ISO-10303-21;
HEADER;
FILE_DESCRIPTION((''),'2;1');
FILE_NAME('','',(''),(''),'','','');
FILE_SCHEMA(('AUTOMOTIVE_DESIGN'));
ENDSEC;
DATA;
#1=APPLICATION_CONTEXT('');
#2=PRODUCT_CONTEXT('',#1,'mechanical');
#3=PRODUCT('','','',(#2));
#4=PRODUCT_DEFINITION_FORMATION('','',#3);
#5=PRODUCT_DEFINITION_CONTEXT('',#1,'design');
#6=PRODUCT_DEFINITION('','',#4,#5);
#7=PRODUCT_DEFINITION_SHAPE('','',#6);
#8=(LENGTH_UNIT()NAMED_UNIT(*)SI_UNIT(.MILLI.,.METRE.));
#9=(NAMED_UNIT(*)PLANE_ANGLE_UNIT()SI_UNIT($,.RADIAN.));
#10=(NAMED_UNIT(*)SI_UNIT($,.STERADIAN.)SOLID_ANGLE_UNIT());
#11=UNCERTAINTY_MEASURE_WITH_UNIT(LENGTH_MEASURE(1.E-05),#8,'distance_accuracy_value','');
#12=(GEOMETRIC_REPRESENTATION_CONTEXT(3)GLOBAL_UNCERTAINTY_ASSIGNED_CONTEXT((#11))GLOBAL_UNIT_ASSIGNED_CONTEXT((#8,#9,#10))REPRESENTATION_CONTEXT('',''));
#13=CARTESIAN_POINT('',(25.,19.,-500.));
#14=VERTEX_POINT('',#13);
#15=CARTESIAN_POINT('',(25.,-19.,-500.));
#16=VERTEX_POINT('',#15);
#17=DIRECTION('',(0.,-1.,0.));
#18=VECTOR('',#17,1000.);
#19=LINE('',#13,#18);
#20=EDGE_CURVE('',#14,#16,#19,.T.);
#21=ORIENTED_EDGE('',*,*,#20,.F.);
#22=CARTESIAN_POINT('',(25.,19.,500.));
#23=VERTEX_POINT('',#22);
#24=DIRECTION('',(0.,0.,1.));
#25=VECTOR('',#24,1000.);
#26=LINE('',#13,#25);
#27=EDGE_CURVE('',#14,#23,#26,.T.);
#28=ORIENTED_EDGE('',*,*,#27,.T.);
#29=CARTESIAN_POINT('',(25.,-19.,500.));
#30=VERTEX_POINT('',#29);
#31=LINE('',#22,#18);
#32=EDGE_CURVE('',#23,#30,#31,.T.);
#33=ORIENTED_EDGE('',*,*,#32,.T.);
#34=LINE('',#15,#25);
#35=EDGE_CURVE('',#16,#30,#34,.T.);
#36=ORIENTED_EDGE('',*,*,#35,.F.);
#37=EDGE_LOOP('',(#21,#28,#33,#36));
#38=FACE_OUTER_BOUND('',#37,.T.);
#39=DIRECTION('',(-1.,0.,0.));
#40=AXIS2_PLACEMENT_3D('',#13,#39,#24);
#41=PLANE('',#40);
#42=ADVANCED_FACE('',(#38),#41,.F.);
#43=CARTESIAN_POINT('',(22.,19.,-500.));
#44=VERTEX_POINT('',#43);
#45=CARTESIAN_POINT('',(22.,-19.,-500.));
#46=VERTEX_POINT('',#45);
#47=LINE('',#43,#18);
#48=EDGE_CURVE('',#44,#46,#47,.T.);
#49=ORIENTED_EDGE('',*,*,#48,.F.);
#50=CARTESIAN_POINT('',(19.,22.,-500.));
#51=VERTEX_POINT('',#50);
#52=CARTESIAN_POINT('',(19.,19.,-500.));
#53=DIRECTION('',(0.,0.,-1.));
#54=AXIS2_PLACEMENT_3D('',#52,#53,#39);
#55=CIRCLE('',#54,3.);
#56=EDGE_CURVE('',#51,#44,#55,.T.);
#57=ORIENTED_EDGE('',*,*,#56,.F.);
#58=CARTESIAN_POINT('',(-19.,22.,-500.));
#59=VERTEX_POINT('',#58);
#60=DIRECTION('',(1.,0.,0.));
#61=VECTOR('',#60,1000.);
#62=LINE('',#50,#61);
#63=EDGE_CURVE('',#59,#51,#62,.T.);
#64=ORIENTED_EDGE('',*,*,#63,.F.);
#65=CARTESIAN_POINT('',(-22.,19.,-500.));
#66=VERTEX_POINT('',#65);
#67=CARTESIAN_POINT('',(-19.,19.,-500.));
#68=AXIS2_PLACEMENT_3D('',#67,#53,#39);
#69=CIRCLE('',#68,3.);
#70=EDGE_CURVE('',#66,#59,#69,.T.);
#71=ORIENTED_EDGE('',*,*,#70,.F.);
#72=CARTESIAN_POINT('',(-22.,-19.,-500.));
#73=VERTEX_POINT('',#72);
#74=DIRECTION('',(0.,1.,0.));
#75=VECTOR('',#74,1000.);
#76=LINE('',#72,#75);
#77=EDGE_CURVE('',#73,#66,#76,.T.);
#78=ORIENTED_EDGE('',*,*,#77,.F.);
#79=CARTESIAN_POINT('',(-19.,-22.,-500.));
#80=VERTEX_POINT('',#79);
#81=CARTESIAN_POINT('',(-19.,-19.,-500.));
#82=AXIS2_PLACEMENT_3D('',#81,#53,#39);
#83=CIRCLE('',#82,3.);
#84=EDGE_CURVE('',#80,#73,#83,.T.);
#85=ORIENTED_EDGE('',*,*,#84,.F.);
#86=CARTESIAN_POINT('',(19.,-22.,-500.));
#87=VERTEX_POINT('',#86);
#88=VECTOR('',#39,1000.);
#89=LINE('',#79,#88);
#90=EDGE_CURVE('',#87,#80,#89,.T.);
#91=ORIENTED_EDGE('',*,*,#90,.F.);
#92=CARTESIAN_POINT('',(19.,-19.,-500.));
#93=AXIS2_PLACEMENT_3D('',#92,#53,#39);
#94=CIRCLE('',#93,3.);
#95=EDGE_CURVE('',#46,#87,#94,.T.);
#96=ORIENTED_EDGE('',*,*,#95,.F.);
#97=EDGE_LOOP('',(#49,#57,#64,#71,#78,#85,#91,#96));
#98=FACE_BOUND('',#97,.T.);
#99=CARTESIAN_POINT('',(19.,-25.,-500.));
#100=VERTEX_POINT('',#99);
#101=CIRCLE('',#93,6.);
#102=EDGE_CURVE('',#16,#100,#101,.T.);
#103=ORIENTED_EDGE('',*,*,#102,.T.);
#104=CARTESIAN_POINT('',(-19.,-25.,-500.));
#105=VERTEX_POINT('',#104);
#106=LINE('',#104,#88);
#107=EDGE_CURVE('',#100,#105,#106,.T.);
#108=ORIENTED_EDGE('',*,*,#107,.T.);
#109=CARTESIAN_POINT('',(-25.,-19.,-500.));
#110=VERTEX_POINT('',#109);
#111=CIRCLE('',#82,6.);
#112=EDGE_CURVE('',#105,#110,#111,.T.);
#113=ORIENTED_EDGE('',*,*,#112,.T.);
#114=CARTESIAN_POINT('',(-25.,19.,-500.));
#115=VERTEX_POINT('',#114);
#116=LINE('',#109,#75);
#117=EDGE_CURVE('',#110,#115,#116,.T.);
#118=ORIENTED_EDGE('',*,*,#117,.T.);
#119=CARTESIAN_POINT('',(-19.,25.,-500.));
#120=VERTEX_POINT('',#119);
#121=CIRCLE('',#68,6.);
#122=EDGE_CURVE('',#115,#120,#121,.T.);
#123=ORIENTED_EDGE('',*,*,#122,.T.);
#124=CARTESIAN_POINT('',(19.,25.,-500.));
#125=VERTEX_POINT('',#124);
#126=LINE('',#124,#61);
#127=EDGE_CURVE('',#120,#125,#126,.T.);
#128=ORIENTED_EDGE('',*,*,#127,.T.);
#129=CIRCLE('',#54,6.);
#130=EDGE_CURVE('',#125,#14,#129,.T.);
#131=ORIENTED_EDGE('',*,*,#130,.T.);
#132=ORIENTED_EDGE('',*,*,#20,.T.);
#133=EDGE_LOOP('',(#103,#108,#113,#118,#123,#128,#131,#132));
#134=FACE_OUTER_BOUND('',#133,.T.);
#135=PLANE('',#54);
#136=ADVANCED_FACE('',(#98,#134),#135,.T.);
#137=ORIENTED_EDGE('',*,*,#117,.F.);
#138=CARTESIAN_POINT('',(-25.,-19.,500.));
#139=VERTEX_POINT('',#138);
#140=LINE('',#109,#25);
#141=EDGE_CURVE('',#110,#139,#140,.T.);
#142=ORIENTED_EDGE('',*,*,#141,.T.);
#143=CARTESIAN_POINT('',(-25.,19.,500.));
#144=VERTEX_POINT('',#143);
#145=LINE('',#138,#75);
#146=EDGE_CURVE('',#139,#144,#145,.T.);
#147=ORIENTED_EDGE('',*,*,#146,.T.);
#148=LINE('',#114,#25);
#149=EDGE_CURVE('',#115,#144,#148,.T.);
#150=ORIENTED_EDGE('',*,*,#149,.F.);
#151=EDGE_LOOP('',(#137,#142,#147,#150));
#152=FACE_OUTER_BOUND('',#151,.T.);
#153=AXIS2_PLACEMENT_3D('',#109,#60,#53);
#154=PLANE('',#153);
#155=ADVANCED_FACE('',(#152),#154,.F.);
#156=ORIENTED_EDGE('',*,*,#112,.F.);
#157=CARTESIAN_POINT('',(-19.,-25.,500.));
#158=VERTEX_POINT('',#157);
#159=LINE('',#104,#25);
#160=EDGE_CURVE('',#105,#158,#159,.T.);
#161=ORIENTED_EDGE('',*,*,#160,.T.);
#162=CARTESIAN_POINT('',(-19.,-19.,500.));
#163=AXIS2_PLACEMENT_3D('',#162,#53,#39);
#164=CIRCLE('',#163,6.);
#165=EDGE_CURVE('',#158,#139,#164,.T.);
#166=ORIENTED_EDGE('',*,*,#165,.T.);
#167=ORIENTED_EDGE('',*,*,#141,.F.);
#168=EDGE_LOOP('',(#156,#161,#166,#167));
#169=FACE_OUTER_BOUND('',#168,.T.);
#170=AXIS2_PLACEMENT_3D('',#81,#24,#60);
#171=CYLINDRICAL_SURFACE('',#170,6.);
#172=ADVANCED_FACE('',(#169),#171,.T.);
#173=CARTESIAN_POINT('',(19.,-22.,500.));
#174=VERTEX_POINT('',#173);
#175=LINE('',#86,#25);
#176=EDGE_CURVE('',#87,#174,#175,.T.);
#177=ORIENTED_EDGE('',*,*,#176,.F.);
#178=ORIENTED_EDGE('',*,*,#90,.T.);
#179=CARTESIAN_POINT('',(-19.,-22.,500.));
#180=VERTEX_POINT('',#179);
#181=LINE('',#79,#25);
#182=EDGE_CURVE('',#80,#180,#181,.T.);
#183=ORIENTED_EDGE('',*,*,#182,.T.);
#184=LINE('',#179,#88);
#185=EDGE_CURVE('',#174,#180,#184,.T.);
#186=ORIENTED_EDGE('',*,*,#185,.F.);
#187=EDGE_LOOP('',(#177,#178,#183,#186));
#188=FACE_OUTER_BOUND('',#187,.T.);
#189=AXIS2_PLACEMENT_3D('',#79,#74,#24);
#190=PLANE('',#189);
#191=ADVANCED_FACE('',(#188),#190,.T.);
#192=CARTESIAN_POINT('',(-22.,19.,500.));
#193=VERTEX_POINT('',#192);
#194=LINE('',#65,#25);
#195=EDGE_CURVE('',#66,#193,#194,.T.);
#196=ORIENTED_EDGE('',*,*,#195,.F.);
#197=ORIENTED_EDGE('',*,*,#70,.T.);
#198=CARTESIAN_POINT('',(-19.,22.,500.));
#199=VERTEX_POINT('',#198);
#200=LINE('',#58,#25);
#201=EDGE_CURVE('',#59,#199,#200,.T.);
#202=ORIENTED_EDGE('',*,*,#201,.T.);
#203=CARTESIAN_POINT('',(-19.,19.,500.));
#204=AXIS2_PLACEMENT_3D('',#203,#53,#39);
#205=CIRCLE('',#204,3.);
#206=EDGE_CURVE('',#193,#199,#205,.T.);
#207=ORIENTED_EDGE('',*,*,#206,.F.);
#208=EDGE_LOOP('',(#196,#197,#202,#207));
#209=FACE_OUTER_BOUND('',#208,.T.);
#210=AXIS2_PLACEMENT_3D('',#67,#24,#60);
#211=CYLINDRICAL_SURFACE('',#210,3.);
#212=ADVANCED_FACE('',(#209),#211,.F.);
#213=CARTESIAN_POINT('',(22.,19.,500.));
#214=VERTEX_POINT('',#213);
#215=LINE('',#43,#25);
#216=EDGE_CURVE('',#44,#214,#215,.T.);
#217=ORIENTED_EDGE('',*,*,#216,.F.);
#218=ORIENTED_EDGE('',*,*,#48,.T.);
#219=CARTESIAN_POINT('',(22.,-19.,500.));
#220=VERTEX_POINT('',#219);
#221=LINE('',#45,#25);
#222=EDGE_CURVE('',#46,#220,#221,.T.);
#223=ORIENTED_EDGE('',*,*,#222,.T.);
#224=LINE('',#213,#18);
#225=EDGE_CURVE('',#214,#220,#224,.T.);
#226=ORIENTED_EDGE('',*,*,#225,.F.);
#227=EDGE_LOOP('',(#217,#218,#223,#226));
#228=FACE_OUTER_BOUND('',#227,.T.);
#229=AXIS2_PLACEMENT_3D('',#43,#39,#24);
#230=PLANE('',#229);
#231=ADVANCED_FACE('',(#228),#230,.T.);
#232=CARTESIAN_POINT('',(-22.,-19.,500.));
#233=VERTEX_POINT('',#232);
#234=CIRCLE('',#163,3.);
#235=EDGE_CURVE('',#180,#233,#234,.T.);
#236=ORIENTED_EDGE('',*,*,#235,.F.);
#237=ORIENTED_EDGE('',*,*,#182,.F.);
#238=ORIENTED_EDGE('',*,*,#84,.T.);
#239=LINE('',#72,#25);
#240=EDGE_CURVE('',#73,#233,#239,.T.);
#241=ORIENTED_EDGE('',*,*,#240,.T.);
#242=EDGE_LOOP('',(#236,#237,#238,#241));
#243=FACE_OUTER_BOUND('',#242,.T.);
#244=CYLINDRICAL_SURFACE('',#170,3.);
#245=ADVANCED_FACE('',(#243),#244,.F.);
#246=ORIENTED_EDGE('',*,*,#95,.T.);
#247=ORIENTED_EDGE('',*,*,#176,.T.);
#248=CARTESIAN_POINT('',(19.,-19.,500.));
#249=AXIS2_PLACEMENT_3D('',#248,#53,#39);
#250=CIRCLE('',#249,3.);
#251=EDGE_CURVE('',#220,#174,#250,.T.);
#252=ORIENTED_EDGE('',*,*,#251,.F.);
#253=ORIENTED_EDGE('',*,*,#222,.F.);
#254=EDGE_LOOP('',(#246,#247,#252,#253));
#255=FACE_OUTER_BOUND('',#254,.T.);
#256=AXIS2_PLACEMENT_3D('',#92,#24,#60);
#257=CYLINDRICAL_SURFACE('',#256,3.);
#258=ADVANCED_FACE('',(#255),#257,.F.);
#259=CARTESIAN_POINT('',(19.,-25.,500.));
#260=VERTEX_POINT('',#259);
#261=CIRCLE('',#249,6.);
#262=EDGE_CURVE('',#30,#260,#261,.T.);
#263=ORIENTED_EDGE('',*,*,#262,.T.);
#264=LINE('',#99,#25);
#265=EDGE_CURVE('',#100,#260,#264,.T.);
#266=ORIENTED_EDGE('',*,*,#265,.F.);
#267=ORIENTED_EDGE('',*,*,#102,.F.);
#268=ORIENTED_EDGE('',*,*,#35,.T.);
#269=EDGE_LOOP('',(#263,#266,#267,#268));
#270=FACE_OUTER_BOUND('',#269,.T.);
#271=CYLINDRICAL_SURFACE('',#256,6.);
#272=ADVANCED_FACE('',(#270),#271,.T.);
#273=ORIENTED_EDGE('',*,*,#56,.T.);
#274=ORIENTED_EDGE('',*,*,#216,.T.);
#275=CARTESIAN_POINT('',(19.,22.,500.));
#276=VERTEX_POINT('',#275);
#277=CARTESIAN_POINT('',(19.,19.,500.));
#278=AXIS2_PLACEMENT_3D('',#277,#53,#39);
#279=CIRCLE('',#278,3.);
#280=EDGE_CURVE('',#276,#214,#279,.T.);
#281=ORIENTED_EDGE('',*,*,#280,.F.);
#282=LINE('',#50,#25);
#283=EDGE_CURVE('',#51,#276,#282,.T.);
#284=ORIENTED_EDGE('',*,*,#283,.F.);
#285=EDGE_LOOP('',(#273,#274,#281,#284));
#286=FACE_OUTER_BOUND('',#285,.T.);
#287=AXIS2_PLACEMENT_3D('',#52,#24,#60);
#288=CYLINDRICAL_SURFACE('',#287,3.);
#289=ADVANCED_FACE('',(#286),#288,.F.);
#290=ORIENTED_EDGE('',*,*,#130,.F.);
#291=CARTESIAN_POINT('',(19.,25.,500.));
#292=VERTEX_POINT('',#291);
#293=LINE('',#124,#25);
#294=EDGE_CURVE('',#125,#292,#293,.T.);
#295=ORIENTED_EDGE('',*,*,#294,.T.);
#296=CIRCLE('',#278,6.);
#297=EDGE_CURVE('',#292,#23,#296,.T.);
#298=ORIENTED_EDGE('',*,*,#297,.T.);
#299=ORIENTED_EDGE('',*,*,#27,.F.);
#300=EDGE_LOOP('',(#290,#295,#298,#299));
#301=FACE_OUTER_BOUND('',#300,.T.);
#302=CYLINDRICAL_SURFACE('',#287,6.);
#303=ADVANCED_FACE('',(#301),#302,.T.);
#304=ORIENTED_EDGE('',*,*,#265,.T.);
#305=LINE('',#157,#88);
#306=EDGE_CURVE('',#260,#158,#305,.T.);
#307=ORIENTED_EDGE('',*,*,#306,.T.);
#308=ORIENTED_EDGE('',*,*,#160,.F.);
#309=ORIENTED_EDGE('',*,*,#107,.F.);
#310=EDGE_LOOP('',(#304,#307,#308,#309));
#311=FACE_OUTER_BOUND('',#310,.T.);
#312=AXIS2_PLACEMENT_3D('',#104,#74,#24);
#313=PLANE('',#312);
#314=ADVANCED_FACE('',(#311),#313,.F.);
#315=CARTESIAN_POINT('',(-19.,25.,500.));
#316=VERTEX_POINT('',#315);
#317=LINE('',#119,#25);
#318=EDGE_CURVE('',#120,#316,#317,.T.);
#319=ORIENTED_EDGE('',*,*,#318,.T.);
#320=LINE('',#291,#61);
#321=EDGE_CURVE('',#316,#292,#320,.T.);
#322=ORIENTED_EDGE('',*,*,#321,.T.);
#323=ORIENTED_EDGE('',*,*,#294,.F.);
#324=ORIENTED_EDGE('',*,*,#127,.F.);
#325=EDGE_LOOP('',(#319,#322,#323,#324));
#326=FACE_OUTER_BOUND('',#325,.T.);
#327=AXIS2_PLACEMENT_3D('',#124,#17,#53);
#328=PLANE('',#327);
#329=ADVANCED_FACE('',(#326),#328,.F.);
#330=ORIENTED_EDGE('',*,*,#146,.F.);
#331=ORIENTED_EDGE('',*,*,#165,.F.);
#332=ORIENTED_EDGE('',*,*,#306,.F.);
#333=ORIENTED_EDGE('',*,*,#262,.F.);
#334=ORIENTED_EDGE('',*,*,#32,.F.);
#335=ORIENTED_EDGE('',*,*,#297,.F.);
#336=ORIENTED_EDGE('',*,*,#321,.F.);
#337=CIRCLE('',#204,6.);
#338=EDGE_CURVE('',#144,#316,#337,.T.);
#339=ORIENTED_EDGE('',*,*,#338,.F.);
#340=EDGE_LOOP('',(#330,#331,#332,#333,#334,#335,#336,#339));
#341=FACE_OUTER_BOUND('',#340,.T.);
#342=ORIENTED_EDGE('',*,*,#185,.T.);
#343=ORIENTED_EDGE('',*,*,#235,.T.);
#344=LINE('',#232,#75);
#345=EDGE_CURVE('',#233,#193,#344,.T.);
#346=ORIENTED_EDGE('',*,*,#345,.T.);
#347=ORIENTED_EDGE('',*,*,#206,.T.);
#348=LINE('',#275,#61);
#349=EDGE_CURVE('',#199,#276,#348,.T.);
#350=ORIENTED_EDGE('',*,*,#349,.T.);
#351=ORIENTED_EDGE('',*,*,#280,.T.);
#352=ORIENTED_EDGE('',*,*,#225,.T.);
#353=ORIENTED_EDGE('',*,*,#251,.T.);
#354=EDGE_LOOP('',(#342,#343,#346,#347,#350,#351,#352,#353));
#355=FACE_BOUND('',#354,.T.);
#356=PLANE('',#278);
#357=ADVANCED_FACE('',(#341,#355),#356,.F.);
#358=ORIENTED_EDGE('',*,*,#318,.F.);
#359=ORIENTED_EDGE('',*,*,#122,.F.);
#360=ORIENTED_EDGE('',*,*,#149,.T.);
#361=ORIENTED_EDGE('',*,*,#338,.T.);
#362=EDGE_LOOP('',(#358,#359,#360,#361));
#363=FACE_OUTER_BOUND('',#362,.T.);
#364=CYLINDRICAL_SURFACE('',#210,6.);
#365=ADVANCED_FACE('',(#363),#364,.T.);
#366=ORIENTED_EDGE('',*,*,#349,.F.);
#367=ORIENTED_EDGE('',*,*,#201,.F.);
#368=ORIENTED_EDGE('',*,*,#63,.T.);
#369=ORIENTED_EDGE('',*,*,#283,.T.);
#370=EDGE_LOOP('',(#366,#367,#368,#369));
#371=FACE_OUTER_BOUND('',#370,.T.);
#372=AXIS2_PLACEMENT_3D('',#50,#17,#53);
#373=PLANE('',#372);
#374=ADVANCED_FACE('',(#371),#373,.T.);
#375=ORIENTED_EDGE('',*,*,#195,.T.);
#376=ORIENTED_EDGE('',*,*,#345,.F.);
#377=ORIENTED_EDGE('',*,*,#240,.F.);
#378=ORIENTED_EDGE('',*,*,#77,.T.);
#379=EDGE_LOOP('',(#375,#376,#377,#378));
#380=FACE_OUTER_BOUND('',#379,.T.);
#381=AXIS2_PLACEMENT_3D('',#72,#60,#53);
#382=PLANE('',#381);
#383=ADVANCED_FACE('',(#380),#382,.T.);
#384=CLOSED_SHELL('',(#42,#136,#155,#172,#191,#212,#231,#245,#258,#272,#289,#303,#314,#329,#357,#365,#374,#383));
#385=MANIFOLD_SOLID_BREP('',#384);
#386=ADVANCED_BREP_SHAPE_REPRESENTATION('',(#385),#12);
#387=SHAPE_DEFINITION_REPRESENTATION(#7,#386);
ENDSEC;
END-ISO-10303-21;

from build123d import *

# Parameters (mm, degrees)
GB_6728_1986_050_X_50_X_3_1_DEPTH = 1000


with BuildPart() as part:
    # Sketch1 → Gb／6728-1986方形空心型钢 050 X 50 X 3(1) (new body)
    with BuildSketch(Plane.YX.offset(-500)):
        with BuildLine():
            Line((-19, -25), (19, -25))
            ThreePointArc((19, -25), (23.242640687, -23.242640687), (25, -19))
            Line((25, -19), (25, 19))
            ThreePointArc((25, 19), (23.242640687, 23.242640687), (19, 25))
            Line((19, 25), (-19, 25))
            ThreePointArc((-19, 25), (-23.242640687, 23.242640687), (-25, 19))
            Line((-25, 19), (-25, -19))
            ThreePointArc((-25, -19), (-23.242640687, -23.242640687), (-19, -25))
        make_face()
        with BuildLine():
            Line((-19, -22), (19, -22))
            ThreePointArc((19, -22), (21.121320344, -21.121320344), (22, -19))
            Line((22, -19), (22, 19))
            ThreePointArc((22, 19), (21.121320344, 21.121320344), (19, 22))
            Line((19, 22), (-19, 22))
            ThreePointArc((-19, 22), (-21.121320344, 21.121320344), (-22, 19))
            Line((-22, 19), (-22, -19))
            ThreePointArc((-22, -19), (-21.121320344, -21.121320344), (-19, -22))
        make_face(mode=Mode.SUBTRACT)
    extrude(amount=GB_6728_1986_050_X_50_X_3_1_DEPTH)


solid = part.part
